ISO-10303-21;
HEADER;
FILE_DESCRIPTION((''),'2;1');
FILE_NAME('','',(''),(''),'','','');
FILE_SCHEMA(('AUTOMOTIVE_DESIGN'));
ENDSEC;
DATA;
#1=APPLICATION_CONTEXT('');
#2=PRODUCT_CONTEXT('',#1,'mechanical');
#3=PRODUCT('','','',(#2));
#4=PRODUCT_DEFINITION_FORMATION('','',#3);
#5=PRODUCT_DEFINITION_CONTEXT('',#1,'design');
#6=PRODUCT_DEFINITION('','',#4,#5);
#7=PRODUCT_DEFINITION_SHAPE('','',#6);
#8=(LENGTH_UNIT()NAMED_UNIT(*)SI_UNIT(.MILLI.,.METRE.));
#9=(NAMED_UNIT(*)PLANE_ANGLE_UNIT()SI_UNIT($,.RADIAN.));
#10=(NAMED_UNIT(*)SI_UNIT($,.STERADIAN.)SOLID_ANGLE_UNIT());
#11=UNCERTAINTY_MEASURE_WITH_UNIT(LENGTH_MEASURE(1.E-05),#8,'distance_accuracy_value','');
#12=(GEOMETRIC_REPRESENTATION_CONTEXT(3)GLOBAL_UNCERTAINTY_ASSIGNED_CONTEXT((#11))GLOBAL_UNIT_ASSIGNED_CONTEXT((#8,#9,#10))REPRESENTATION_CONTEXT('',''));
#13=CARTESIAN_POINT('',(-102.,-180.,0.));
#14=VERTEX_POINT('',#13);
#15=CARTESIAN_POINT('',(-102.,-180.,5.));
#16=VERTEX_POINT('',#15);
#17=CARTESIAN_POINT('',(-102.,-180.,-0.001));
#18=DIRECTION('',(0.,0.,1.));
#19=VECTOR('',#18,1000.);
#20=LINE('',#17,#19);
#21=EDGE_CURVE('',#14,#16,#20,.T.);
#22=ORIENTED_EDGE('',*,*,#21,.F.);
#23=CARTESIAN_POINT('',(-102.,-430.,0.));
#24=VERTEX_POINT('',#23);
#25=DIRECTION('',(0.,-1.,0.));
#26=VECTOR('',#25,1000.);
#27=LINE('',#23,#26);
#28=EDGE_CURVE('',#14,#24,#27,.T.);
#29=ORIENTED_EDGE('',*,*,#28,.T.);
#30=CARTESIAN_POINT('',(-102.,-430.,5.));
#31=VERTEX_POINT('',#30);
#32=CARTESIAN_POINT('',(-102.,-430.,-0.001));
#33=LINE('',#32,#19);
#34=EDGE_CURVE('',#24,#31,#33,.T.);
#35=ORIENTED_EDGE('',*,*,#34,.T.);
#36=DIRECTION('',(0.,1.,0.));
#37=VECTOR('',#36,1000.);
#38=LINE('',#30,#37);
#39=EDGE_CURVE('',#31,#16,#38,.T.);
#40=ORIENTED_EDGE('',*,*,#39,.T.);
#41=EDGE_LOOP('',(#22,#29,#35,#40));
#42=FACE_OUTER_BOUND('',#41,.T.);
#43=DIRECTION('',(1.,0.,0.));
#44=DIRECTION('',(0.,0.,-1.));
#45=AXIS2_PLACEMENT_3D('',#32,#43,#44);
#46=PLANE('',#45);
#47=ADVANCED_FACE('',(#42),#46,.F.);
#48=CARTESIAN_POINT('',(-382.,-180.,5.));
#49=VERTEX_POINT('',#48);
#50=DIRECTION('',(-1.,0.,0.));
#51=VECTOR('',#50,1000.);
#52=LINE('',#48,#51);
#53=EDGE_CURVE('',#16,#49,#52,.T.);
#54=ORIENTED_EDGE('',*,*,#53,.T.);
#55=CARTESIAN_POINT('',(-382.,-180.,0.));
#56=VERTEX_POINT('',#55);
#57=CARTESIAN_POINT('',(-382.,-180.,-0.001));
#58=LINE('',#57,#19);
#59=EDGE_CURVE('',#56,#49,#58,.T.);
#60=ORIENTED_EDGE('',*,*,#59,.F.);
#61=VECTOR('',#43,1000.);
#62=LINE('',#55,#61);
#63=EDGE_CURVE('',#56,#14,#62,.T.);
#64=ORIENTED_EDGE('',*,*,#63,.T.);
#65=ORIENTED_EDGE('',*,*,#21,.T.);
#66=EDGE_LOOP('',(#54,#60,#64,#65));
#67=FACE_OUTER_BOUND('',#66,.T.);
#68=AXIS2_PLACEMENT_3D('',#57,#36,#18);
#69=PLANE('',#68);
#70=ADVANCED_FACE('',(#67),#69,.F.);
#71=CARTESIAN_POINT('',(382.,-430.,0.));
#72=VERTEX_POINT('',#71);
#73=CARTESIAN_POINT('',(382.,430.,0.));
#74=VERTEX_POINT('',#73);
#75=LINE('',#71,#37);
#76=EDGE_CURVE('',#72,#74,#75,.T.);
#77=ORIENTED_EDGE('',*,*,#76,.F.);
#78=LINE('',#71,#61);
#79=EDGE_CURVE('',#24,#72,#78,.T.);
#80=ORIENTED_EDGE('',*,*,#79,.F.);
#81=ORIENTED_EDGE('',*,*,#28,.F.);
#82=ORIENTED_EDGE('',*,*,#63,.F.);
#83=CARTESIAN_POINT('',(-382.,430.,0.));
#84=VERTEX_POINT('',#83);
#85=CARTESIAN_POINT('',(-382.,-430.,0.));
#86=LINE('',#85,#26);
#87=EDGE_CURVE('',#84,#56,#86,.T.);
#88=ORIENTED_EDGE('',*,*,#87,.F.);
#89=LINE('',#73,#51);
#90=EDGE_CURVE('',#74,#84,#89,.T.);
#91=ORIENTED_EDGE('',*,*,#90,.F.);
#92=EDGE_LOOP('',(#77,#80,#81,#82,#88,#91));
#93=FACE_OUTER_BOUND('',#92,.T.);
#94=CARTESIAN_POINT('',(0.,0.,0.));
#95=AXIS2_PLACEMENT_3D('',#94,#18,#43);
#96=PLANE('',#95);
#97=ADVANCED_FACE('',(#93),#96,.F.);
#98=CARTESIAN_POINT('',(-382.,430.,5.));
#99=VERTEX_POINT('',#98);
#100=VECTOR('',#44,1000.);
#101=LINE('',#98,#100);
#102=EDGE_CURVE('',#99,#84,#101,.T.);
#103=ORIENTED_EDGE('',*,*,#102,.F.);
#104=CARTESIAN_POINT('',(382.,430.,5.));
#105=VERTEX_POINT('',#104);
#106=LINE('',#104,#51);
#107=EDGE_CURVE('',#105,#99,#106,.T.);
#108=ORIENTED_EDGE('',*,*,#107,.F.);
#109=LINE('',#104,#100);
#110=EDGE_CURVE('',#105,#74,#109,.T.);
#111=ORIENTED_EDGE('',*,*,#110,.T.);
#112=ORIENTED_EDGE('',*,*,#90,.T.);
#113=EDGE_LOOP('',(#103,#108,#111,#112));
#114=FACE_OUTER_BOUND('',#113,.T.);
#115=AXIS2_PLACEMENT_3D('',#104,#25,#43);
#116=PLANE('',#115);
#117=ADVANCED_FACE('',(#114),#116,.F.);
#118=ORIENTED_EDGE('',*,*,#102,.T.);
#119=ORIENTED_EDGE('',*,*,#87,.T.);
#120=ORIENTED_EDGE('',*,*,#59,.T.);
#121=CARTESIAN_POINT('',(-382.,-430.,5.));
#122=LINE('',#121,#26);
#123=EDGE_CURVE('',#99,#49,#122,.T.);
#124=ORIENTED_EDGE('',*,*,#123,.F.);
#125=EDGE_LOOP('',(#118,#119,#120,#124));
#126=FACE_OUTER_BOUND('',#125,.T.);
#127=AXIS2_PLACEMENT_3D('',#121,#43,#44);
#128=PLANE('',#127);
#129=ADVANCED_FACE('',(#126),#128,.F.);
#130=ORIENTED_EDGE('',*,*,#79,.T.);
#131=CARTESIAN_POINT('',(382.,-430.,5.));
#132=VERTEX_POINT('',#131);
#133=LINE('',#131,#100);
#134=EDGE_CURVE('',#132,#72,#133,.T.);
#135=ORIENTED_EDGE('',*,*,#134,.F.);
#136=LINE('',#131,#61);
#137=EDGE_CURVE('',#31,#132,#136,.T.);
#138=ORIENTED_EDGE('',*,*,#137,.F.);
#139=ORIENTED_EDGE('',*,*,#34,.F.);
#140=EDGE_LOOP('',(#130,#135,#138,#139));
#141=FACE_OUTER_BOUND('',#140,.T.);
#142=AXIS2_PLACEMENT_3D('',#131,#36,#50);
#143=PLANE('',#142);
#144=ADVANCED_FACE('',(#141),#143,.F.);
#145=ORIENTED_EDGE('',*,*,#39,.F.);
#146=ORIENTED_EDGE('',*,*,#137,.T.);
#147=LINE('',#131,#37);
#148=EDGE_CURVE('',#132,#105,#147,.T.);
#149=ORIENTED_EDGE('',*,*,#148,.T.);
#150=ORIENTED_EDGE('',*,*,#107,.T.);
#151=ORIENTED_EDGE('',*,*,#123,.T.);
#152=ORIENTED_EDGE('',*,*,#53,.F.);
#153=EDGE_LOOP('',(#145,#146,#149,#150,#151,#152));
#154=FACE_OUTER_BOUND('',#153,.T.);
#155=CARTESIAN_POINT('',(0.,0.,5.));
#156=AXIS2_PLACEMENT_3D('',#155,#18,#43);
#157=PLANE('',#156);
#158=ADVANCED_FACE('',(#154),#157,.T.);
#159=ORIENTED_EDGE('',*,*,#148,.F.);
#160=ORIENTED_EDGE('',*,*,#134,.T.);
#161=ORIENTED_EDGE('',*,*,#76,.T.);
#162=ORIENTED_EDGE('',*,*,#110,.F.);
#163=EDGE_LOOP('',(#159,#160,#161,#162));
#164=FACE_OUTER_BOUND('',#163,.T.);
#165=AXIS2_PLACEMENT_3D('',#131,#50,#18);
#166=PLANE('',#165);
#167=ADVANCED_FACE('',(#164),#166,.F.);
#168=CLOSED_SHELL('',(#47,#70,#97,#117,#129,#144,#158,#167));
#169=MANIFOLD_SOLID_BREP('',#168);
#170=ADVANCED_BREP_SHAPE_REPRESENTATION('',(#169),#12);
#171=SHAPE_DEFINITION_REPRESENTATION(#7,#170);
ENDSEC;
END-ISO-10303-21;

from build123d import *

# Parameters (mm, degrees)
SKETCH_1_W          = 764
SKETCH_1_H          = 860
EXTRUDE_1_DEPTH     = 5
CUT_EXTRUDE_1_REACH = 577.195
SKETCH_2_W          = 280
SKETCH_2_H          = 250


with BuildPart() as part:
    # 草图1 → 凸台-拉伸1 (new body)
    with BuildSketch(Plane.XY):
        Rectangle(SKETCH_1_W, SKETCH_1_H)
    extrude(amount=EXTRUDE_1_DEPTH)

    # 草图2 → 切除-拉伸1 (cut, up to next)
    with BuildSketch(Plane.XY.offset(5), mode=Mode.PRIVATE) as cut_extrude_1_sk1:
        with Locations((-242, -305)):
            Rectangle(SKETCH_2_W, SKETCH_2_H)
    cut_extrude_1_tool1 = extrude(cut_extrude_1_sk1.sketch, amount=-CUT_EXTRUDE_1_REACH, mode=Mode.PRIVATE) & part.part
    add(cut_extrude_1_tool1.solids().sort_by_distance((-242, -305, 5))[0], mode=Mode.SUBTRACT)


solid = part.part
